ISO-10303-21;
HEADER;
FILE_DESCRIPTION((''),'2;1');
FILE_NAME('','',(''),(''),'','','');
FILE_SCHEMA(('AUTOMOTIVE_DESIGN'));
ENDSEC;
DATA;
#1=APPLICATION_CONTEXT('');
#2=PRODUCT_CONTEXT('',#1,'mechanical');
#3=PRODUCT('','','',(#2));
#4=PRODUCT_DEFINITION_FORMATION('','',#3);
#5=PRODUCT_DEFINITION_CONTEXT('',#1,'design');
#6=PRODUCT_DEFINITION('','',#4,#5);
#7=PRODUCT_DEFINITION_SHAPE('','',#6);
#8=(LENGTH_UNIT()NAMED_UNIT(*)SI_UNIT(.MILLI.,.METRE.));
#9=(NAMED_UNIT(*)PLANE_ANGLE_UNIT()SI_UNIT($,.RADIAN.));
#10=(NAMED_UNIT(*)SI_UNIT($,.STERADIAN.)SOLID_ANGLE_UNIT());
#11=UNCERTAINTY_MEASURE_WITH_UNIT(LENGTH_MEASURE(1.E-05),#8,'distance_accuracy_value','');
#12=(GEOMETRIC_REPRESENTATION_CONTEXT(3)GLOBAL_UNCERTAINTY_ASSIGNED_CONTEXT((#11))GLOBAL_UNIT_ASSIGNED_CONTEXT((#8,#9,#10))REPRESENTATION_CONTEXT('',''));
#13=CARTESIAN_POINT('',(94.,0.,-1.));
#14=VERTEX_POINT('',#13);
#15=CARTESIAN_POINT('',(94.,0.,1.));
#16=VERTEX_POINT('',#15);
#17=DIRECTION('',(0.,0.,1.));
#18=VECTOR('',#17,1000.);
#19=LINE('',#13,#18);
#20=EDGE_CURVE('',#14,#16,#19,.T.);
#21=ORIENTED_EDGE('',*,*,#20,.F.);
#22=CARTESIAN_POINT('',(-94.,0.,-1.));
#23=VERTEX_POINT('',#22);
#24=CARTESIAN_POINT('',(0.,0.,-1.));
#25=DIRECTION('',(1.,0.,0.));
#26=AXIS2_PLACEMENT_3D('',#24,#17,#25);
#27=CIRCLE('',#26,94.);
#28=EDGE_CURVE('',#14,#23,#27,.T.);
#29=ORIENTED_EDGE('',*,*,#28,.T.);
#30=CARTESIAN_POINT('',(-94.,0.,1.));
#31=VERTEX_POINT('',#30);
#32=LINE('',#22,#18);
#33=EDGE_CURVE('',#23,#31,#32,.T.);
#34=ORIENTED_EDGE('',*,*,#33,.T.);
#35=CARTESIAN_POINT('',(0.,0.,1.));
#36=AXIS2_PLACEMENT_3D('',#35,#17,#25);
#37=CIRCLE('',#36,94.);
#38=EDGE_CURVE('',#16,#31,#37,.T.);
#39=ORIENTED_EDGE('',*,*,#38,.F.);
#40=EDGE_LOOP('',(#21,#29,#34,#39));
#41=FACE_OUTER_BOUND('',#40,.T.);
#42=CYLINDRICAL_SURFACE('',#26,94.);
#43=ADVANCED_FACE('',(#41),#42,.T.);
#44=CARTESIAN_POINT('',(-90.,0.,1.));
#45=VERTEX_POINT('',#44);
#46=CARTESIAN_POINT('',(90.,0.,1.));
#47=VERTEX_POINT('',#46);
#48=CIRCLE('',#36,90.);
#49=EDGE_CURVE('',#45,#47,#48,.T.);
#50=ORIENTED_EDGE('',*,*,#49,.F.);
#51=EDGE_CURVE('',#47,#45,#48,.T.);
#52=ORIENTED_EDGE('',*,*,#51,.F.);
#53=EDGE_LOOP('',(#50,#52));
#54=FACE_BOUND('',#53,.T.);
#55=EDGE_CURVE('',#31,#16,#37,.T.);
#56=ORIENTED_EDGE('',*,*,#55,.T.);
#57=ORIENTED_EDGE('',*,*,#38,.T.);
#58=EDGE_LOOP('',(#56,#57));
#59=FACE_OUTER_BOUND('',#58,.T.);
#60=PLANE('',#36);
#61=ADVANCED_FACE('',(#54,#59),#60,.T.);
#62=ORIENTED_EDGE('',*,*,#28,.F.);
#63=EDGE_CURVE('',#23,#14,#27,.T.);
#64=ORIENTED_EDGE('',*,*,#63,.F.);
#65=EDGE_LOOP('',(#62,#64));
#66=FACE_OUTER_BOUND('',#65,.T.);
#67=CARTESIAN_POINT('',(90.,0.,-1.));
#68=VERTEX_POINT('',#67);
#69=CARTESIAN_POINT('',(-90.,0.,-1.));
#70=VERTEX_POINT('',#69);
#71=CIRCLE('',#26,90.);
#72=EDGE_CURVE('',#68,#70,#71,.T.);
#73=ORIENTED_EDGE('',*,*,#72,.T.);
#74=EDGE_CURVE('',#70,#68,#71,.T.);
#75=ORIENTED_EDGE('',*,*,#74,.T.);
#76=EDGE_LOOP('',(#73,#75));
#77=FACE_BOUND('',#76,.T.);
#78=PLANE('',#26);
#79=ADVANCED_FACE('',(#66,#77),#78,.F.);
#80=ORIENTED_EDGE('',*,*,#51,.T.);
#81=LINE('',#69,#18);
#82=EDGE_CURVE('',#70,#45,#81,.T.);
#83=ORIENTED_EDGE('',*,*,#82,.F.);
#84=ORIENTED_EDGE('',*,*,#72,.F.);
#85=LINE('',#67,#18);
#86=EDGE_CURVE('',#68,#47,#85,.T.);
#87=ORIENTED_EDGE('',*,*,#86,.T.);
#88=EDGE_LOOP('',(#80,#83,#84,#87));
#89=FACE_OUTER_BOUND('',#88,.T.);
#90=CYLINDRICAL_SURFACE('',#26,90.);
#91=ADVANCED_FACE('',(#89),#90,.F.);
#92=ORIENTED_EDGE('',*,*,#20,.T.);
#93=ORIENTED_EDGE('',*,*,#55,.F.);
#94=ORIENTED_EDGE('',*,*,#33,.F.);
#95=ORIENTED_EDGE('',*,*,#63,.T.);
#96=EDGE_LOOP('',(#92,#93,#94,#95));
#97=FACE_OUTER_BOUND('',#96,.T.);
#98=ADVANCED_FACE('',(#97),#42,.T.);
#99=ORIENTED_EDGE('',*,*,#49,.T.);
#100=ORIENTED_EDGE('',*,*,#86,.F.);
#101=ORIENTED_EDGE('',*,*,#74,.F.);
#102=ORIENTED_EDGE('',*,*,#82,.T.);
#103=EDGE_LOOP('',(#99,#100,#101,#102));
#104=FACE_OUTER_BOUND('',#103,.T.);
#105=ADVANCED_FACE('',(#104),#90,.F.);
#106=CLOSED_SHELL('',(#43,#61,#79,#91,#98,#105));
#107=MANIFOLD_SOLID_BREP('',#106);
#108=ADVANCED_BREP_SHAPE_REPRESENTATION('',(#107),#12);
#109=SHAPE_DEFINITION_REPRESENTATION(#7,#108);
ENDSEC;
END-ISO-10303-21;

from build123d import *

# Parameters (mm, degrees)
SKETCH_1_R      = 94
SKETCH_1_R_2    = 90
EXTRUDE_1_DEPTH = 1


with BuildPart() as part:
    # 草图1 → 凸台-拉伸1 (new, symmetric)
    with BuildSketch(Plane.XY):
        Circle(SKETCH_1_R)
        Circle(SKETCH_1_R_2, mode=Mode.SUBTRACT)
    extrude(amount=EXTRUDE_1_DEPTH, both=True)


solid = part.part
